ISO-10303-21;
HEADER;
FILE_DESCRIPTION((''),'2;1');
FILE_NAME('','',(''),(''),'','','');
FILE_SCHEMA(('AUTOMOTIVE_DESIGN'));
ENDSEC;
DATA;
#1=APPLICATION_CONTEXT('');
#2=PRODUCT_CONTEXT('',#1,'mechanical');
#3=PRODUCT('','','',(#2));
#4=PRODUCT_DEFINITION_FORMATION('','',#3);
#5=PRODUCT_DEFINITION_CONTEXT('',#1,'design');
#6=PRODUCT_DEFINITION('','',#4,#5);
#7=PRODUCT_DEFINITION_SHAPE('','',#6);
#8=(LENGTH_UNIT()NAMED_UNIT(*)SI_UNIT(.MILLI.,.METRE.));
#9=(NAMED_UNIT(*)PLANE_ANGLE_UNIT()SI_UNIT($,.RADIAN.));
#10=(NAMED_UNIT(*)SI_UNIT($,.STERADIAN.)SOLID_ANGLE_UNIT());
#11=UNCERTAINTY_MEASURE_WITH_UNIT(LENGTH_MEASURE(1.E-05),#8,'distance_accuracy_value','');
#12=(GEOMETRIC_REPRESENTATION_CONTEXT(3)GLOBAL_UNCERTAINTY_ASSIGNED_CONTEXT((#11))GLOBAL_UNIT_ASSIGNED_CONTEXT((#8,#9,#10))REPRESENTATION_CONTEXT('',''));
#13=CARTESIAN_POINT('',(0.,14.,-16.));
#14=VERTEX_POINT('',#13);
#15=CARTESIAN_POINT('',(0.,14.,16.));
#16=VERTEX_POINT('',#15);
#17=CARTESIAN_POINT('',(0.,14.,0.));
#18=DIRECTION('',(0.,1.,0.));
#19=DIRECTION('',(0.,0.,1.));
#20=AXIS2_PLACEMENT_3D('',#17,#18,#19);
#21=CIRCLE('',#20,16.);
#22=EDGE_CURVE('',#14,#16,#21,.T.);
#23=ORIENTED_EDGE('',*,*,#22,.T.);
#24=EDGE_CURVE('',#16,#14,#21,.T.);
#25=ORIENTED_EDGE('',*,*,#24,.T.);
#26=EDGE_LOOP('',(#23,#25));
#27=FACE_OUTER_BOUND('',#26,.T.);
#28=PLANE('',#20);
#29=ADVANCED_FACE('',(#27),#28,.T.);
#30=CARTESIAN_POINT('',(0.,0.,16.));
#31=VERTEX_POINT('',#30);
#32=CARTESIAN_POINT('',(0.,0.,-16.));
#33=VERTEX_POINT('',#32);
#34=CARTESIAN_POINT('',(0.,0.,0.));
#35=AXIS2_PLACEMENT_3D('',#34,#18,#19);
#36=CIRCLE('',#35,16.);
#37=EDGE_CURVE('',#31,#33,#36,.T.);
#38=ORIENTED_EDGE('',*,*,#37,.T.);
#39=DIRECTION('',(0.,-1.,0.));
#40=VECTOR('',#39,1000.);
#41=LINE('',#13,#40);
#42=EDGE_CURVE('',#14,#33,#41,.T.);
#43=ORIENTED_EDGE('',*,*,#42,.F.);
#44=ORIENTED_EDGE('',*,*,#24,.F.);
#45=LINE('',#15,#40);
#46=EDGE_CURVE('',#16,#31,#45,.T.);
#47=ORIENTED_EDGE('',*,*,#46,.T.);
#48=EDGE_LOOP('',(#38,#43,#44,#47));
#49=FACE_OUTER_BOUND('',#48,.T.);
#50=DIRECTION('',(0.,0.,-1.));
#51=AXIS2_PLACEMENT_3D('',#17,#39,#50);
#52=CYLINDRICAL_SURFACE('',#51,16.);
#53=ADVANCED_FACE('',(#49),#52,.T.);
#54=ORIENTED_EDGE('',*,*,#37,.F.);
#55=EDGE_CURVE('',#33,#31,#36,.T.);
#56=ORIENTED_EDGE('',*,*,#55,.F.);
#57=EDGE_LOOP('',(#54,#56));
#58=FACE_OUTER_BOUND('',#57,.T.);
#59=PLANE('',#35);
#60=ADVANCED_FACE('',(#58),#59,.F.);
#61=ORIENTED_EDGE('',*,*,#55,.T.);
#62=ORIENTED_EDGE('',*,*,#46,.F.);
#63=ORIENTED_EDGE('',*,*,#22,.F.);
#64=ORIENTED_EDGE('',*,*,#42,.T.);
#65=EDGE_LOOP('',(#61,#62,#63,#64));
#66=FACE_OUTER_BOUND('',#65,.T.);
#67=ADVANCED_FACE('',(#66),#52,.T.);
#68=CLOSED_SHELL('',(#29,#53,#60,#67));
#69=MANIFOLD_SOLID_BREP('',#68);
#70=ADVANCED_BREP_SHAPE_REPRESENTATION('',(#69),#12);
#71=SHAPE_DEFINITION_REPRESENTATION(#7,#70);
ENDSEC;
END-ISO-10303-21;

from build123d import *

# Parameters (mm, degrees)
SKETCH1_R           = 16
BOSS_EXTRUDE1_DEPTH = 14


with BuildPart() as part:
    # Sketch1 → Boss-Extrude1 (new body)
    with BuildSketch(Plane(origin=(0, 0, 0), x_dir=(1, 0, 0), z_dir=(0, 1, 0))):
        with Locations(Location((0, 0, 0), (0, 0, 270))):
            Circle(SKETCH1_R)
    extrude(amount=BOSS_EXTRUDE1_DEPTH)


solid = part.part
